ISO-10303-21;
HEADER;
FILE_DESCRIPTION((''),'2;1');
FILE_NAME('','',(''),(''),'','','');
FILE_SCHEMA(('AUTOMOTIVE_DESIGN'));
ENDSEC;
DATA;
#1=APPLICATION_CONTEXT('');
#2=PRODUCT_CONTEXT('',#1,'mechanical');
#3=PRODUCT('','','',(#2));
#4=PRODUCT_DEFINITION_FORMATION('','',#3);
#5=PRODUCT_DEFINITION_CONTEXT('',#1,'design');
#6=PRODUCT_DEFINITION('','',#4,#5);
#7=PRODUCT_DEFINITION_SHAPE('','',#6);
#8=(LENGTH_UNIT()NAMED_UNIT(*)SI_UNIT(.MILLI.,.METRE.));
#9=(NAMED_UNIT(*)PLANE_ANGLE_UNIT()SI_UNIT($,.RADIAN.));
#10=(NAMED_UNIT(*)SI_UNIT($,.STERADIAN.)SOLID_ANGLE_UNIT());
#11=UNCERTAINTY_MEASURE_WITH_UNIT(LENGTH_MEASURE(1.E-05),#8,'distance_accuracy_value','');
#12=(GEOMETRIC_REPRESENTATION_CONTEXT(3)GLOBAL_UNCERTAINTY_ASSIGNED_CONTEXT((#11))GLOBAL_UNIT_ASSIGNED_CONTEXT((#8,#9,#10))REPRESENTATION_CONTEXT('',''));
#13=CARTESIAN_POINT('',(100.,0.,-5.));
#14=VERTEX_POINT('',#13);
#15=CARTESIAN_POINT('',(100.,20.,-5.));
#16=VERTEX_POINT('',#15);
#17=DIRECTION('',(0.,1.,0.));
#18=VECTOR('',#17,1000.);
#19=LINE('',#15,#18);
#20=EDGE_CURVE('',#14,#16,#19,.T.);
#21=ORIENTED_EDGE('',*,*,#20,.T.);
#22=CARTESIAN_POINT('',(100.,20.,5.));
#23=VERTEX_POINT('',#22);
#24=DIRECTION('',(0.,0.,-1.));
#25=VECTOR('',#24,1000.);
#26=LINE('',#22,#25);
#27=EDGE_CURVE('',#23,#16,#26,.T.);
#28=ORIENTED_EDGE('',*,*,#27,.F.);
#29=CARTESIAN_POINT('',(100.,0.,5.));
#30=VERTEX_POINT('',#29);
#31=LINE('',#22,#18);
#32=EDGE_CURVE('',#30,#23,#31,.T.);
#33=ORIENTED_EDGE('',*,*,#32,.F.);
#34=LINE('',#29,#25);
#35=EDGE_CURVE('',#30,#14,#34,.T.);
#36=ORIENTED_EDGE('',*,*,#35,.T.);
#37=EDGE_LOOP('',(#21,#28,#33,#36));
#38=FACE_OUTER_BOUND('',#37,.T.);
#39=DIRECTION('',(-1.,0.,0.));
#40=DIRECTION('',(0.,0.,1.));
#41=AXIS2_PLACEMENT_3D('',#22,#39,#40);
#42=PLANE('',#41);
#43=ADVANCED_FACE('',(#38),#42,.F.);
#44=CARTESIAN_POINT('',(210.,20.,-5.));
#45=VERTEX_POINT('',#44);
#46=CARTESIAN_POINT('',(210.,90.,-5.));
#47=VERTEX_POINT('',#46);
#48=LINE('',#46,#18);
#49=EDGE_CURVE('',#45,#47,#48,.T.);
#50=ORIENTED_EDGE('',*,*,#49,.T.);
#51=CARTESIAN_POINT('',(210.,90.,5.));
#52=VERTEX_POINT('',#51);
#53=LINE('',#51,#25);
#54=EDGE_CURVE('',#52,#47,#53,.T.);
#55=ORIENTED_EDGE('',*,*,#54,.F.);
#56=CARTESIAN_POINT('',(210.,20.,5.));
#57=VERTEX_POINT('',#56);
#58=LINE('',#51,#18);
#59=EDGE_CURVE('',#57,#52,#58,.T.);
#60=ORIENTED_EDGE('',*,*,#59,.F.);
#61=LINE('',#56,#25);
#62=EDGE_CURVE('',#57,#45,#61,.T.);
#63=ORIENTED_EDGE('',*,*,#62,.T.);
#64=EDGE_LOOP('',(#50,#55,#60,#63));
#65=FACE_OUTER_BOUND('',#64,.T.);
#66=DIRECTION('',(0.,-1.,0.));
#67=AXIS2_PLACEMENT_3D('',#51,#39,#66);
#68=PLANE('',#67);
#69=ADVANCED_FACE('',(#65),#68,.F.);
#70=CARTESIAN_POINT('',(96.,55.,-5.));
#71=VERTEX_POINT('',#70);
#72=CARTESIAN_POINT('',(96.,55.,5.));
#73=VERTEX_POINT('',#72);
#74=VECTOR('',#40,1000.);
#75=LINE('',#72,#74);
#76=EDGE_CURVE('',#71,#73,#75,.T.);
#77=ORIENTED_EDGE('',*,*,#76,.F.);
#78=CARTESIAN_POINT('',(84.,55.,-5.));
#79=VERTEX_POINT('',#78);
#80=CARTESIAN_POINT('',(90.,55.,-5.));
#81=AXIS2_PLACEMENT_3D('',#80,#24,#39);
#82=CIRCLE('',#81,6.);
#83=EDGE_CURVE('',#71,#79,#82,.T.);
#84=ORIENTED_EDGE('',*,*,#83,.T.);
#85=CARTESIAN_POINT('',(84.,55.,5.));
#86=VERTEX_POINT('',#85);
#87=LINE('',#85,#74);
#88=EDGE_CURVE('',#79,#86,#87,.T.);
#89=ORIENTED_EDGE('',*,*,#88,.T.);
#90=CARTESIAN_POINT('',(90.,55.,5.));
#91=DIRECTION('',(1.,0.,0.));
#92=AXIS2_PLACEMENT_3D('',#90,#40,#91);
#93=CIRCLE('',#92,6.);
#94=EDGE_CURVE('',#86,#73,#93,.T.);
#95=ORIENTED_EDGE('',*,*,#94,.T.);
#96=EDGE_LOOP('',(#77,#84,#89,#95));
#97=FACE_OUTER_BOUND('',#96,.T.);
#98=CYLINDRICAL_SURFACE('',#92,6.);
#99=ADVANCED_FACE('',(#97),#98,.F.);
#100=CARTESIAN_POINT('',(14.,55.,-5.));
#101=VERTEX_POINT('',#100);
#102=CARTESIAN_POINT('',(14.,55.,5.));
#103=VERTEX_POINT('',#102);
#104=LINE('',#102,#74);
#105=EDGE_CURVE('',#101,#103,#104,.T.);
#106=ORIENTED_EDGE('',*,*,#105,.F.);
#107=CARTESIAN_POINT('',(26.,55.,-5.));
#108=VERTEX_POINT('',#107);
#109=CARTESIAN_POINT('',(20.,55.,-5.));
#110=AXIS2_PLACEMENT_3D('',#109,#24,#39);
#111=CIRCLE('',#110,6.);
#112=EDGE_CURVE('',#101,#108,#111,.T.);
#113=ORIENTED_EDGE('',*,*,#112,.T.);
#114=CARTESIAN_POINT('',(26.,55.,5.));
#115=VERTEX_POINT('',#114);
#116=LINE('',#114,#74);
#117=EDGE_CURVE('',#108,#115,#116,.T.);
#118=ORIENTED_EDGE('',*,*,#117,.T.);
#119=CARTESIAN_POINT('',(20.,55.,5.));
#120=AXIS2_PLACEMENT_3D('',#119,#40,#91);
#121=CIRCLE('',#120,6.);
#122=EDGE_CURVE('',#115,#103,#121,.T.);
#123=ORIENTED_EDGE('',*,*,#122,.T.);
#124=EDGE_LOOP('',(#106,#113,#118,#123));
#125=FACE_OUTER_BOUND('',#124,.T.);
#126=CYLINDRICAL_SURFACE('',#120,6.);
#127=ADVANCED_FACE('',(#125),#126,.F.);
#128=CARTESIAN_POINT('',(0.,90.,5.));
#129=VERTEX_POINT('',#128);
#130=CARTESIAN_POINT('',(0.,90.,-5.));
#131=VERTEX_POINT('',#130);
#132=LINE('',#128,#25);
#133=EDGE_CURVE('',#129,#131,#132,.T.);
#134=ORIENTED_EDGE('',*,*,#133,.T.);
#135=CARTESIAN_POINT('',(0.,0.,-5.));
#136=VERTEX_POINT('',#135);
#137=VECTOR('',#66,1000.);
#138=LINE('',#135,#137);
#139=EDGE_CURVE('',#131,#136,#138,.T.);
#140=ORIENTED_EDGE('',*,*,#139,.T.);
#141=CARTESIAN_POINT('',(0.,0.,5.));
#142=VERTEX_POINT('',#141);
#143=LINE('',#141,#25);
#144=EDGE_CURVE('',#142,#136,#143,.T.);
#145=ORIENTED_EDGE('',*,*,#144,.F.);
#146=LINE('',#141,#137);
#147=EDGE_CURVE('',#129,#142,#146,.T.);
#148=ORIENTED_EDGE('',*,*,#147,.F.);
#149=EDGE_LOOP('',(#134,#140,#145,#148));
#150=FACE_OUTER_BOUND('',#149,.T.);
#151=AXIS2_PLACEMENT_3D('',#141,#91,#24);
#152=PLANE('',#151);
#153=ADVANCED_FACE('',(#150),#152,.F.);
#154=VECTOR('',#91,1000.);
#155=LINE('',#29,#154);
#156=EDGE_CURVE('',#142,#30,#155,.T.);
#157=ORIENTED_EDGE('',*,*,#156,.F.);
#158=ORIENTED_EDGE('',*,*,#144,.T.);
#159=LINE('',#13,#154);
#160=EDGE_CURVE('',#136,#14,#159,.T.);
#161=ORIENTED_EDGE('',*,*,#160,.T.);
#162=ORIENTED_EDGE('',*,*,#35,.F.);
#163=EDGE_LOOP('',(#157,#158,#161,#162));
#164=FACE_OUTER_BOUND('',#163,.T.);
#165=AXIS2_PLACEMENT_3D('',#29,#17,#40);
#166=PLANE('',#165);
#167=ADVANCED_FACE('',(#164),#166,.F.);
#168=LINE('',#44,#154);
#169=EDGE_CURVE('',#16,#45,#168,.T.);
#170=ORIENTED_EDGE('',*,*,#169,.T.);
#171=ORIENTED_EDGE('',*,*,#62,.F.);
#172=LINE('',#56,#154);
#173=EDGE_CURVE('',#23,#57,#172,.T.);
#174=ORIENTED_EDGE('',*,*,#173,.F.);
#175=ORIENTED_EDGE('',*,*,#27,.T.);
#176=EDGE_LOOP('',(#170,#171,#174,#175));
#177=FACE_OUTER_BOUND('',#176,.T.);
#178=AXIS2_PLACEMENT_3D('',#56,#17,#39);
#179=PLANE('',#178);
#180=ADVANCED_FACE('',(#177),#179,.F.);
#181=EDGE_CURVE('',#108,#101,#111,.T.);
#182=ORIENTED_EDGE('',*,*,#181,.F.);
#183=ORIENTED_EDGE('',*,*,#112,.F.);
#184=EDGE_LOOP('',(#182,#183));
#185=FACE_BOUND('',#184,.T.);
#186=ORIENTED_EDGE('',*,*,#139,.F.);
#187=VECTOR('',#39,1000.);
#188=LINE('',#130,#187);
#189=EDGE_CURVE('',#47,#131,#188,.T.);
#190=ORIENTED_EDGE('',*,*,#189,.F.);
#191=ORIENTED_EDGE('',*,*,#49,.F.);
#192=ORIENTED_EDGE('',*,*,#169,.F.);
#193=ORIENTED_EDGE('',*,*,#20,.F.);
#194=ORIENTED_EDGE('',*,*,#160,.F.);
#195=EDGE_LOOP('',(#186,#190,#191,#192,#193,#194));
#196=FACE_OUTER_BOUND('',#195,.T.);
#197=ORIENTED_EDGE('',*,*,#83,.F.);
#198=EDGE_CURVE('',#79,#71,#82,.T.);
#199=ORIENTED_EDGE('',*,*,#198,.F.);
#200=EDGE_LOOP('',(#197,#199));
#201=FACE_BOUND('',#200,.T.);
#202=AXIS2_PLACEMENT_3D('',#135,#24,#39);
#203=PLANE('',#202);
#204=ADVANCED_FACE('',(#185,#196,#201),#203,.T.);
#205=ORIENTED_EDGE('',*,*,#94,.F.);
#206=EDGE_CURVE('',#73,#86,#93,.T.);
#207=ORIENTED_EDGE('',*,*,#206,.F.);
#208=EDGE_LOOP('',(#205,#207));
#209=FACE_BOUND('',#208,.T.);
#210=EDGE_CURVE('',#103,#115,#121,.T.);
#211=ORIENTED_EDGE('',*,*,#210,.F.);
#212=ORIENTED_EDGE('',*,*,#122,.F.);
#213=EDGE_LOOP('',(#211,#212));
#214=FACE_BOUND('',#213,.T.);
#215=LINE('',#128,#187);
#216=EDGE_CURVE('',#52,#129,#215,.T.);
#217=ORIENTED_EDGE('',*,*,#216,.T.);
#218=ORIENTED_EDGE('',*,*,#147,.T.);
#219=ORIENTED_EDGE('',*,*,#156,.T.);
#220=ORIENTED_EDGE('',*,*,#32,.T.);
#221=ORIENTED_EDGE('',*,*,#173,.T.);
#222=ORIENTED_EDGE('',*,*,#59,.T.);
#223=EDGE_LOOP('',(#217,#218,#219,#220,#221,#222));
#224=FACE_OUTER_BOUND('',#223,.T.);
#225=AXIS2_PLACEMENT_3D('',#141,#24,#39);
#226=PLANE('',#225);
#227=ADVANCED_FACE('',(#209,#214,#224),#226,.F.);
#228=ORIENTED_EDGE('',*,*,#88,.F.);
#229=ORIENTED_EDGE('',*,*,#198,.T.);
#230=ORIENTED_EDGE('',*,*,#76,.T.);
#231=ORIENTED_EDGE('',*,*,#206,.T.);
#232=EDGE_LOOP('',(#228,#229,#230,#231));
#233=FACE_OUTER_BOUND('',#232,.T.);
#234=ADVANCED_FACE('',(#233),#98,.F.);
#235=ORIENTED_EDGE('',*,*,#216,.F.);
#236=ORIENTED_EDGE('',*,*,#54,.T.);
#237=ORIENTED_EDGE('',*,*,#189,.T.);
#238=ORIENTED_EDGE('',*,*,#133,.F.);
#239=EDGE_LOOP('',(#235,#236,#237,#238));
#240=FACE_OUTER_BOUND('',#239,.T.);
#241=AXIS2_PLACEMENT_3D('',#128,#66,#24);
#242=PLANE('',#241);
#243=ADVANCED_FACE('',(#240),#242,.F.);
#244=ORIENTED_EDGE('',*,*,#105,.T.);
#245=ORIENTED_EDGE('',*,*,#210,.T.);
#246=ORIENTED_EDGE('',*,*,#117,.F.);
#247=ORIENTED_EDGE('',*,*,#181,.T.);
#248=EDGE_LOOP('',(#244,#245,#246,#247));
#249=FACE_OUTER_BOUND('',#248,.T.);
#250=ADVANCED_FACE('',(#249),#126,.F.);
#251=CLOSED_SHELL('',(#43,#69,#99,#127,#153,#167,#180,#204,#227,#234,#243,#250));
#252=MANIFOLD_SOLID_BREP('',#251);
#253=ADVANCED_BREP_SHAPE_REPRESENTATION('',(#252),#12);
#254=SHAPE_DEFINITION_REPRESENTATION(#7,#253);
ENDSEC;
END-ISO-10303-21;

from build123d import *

# Parameters (mm, degrees)
BOSS_EXTRUDE1_DEPTH        = 5
F_12_0_12_DIAMETER_HOLE1_D = 12


with BuildPart() as part:
    # Sketch1 → Boss-Extrude1 (new, symmetric)
    with BuildSketch(Plane.XY):
        Polygon((0, 0), (0, 90), (210, 90), (210, 20), (100, 20), (100, 0), align=None)
    extrude(amount=BOSS_EXTRUDE1_DEPTH, both=True)

    # Ø12.0 (12) Diameter Hole1 (through all)
    with Locations(Plane.XY.offset(5)):
        with Locations((20, 55), (90, 55)):
            Hole(F_12_0_12_DIAMETER_HOLE1_D / 2)


solid = part.part
